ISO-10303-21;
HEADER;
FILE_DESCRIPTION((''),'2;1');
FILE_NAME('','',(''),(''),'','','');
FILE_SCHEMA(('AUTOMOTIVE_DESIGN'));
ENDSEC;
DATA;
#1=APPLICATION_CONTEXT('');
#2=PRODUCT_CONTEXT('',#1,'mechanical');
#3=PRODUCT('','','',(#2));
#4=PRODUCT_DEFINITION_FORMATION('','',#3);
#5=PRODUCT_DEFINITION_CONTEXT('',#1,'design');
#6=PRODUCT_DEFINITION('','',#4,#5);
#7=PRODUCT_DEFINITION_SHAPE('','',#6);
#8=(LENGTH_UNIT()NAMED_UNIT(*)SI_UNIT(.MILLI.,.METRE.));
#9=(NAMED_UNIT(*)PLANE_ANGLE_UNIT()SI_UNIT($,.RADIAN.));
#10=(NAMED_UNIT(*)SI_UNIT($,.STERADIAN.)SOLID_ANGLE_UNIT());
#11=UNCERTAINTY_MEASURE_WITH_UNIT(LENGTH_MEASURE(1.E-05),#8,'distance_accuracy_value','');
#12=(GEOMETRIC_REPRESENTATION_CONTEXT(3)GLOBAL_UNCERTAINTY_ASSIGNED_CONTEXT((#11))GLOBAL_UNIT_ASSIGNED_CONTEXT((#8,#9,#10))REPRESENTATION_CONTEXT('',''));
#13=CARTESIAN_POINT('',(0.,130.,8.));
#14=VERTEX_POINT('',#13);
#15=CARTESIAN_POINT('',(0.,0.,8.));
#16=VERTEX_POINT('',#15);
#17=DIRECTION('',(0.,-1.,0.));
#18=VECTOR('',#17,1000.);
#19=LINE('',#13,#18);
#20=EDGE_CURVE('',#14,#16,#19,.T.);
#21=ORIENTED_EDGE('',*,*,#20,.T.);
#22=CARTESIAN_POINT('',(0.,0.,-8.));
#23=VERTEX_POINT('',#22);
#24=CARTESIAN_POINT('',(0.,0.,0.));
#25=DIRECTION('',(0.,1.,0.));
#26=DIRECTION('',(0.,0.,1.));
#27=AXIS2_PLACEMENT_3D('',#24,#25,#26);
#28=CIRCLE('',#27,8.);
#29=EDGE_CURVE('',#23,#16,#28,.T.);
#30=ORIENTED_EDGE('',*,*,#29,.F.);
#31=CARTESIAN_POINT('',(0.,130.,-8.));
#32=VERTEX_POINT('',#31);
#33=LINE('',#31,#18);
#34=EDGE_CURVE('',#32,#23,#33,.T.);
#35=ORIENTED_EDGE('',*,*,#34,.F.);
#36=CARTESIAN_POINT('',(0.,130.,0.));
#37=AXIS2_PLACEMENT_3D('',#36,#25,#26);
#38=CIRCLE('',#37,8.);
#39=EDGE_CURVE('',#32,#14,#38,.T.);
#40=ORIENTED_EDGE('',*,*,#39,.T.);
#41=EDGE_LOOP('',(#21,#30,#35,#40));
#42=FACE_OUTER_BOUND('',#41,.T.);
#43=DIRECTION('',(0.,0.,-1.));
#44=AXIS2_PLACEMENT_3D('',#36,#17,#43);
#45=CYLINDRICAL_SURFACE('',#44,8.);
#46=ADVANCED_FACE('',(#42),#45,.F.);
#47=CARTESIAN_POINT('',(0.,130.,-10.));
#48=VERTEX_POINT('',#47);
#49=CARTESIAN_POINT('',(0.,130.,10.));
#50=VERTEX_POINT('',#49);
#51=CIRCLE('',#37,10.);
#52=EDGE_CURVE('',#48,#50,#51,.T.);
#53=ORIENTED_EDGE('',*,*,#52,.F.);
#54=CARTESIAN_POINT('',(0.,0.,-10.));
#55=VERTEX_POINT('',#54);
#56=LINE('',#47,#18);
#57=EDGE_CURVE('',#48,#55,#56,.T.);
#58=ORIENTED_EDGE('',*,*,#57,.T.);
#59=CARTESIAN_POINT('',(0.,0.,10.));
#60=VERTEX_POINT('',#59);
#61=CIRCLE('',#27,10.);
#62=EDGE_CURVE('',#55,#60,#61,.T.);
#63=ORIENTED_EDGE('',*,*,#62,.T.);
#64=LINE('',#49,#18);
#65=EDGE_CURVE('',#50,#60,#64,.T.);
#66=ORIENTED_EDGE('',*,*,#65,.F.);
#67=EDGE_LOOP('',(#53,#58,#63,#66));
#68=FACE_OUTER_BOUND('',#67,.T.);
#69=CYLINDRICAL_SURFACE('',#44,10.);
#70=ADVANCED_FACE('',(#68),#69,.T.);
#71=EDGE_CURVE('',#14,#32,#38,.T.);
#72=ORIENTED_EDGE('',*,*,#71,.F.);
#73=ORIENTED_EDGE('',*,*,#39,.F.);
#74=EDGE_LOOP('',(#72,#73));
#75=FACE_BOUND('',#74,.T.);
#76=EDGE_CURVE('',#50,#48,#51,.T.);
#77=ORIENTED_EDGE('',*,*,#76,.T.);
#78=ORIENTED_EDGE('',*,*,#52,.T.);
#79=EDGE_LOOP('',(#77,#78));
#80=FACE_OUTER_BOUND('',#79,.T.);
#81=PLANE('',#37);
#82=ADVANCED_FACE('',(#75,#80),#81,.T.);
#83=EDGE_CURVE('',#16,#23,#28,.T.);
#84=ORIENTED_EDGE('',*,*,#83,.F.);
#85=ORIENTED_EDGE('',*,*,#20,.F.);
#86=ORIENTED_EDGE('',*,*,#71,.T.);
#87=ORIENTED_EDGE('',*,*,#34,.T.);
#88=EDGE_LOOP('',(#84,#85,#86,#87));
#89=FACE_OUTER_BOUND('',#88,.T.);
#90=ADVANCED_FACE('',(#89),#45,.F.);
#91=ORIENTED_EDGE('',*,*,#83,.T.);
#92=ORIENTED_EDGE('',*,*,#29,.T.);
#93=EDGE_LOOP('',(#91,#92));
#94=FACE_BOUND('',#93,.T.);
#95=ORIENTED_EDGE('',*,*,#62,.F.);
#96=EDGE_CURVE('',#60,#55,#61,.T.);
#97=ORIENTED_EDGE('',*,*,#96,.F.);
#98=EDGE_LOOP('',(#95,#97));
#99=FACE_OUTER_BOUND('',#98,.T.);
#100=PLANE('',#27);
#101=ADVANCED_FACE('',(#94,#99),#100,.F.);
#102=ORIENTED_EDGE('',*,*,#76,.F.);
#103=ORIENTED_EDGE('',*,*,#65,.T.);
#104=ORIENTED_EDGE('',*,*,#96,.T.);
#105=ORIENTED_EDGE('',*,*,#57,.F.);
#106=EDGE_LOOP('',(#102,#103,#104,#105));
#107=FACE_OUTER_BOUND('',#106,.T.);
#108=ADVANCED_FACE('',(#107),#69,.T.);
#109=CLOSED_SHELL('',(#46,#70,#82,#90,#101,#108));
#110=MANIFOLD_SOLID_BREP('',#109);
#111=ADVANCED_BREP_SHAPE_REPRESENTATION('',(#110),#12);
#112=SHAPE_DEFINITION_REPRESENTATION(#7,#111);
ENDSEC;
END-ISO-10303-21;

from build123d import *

# Parameters (mm, degrees)
SKETCH1_R           = 10
SKETCH1_R_2         = 8
BOSS_EXTRUDE1_DEPTH = 130


with BuildPart() as part:
    # Sketch1 → Boss-Extrude1 (new body)
    with BuildSketch(Plane(origin=(0, 0, 0), x_dir=(1, 0, 0), z_dir=(0, 1, 0))):
        with Locations(Location((0, 0, 0), (0, 0, 270))):
            Circle(SKETCH1_R)
        with Locations(Location((0, 0, 0), (0, 0, 270))):
            Circle(SKETCH1_R_2, mode=Mode.SUBTRACT)
    extrude(amount=BOSS_EXTRUDE1_DEPTH)


solid = part.part
